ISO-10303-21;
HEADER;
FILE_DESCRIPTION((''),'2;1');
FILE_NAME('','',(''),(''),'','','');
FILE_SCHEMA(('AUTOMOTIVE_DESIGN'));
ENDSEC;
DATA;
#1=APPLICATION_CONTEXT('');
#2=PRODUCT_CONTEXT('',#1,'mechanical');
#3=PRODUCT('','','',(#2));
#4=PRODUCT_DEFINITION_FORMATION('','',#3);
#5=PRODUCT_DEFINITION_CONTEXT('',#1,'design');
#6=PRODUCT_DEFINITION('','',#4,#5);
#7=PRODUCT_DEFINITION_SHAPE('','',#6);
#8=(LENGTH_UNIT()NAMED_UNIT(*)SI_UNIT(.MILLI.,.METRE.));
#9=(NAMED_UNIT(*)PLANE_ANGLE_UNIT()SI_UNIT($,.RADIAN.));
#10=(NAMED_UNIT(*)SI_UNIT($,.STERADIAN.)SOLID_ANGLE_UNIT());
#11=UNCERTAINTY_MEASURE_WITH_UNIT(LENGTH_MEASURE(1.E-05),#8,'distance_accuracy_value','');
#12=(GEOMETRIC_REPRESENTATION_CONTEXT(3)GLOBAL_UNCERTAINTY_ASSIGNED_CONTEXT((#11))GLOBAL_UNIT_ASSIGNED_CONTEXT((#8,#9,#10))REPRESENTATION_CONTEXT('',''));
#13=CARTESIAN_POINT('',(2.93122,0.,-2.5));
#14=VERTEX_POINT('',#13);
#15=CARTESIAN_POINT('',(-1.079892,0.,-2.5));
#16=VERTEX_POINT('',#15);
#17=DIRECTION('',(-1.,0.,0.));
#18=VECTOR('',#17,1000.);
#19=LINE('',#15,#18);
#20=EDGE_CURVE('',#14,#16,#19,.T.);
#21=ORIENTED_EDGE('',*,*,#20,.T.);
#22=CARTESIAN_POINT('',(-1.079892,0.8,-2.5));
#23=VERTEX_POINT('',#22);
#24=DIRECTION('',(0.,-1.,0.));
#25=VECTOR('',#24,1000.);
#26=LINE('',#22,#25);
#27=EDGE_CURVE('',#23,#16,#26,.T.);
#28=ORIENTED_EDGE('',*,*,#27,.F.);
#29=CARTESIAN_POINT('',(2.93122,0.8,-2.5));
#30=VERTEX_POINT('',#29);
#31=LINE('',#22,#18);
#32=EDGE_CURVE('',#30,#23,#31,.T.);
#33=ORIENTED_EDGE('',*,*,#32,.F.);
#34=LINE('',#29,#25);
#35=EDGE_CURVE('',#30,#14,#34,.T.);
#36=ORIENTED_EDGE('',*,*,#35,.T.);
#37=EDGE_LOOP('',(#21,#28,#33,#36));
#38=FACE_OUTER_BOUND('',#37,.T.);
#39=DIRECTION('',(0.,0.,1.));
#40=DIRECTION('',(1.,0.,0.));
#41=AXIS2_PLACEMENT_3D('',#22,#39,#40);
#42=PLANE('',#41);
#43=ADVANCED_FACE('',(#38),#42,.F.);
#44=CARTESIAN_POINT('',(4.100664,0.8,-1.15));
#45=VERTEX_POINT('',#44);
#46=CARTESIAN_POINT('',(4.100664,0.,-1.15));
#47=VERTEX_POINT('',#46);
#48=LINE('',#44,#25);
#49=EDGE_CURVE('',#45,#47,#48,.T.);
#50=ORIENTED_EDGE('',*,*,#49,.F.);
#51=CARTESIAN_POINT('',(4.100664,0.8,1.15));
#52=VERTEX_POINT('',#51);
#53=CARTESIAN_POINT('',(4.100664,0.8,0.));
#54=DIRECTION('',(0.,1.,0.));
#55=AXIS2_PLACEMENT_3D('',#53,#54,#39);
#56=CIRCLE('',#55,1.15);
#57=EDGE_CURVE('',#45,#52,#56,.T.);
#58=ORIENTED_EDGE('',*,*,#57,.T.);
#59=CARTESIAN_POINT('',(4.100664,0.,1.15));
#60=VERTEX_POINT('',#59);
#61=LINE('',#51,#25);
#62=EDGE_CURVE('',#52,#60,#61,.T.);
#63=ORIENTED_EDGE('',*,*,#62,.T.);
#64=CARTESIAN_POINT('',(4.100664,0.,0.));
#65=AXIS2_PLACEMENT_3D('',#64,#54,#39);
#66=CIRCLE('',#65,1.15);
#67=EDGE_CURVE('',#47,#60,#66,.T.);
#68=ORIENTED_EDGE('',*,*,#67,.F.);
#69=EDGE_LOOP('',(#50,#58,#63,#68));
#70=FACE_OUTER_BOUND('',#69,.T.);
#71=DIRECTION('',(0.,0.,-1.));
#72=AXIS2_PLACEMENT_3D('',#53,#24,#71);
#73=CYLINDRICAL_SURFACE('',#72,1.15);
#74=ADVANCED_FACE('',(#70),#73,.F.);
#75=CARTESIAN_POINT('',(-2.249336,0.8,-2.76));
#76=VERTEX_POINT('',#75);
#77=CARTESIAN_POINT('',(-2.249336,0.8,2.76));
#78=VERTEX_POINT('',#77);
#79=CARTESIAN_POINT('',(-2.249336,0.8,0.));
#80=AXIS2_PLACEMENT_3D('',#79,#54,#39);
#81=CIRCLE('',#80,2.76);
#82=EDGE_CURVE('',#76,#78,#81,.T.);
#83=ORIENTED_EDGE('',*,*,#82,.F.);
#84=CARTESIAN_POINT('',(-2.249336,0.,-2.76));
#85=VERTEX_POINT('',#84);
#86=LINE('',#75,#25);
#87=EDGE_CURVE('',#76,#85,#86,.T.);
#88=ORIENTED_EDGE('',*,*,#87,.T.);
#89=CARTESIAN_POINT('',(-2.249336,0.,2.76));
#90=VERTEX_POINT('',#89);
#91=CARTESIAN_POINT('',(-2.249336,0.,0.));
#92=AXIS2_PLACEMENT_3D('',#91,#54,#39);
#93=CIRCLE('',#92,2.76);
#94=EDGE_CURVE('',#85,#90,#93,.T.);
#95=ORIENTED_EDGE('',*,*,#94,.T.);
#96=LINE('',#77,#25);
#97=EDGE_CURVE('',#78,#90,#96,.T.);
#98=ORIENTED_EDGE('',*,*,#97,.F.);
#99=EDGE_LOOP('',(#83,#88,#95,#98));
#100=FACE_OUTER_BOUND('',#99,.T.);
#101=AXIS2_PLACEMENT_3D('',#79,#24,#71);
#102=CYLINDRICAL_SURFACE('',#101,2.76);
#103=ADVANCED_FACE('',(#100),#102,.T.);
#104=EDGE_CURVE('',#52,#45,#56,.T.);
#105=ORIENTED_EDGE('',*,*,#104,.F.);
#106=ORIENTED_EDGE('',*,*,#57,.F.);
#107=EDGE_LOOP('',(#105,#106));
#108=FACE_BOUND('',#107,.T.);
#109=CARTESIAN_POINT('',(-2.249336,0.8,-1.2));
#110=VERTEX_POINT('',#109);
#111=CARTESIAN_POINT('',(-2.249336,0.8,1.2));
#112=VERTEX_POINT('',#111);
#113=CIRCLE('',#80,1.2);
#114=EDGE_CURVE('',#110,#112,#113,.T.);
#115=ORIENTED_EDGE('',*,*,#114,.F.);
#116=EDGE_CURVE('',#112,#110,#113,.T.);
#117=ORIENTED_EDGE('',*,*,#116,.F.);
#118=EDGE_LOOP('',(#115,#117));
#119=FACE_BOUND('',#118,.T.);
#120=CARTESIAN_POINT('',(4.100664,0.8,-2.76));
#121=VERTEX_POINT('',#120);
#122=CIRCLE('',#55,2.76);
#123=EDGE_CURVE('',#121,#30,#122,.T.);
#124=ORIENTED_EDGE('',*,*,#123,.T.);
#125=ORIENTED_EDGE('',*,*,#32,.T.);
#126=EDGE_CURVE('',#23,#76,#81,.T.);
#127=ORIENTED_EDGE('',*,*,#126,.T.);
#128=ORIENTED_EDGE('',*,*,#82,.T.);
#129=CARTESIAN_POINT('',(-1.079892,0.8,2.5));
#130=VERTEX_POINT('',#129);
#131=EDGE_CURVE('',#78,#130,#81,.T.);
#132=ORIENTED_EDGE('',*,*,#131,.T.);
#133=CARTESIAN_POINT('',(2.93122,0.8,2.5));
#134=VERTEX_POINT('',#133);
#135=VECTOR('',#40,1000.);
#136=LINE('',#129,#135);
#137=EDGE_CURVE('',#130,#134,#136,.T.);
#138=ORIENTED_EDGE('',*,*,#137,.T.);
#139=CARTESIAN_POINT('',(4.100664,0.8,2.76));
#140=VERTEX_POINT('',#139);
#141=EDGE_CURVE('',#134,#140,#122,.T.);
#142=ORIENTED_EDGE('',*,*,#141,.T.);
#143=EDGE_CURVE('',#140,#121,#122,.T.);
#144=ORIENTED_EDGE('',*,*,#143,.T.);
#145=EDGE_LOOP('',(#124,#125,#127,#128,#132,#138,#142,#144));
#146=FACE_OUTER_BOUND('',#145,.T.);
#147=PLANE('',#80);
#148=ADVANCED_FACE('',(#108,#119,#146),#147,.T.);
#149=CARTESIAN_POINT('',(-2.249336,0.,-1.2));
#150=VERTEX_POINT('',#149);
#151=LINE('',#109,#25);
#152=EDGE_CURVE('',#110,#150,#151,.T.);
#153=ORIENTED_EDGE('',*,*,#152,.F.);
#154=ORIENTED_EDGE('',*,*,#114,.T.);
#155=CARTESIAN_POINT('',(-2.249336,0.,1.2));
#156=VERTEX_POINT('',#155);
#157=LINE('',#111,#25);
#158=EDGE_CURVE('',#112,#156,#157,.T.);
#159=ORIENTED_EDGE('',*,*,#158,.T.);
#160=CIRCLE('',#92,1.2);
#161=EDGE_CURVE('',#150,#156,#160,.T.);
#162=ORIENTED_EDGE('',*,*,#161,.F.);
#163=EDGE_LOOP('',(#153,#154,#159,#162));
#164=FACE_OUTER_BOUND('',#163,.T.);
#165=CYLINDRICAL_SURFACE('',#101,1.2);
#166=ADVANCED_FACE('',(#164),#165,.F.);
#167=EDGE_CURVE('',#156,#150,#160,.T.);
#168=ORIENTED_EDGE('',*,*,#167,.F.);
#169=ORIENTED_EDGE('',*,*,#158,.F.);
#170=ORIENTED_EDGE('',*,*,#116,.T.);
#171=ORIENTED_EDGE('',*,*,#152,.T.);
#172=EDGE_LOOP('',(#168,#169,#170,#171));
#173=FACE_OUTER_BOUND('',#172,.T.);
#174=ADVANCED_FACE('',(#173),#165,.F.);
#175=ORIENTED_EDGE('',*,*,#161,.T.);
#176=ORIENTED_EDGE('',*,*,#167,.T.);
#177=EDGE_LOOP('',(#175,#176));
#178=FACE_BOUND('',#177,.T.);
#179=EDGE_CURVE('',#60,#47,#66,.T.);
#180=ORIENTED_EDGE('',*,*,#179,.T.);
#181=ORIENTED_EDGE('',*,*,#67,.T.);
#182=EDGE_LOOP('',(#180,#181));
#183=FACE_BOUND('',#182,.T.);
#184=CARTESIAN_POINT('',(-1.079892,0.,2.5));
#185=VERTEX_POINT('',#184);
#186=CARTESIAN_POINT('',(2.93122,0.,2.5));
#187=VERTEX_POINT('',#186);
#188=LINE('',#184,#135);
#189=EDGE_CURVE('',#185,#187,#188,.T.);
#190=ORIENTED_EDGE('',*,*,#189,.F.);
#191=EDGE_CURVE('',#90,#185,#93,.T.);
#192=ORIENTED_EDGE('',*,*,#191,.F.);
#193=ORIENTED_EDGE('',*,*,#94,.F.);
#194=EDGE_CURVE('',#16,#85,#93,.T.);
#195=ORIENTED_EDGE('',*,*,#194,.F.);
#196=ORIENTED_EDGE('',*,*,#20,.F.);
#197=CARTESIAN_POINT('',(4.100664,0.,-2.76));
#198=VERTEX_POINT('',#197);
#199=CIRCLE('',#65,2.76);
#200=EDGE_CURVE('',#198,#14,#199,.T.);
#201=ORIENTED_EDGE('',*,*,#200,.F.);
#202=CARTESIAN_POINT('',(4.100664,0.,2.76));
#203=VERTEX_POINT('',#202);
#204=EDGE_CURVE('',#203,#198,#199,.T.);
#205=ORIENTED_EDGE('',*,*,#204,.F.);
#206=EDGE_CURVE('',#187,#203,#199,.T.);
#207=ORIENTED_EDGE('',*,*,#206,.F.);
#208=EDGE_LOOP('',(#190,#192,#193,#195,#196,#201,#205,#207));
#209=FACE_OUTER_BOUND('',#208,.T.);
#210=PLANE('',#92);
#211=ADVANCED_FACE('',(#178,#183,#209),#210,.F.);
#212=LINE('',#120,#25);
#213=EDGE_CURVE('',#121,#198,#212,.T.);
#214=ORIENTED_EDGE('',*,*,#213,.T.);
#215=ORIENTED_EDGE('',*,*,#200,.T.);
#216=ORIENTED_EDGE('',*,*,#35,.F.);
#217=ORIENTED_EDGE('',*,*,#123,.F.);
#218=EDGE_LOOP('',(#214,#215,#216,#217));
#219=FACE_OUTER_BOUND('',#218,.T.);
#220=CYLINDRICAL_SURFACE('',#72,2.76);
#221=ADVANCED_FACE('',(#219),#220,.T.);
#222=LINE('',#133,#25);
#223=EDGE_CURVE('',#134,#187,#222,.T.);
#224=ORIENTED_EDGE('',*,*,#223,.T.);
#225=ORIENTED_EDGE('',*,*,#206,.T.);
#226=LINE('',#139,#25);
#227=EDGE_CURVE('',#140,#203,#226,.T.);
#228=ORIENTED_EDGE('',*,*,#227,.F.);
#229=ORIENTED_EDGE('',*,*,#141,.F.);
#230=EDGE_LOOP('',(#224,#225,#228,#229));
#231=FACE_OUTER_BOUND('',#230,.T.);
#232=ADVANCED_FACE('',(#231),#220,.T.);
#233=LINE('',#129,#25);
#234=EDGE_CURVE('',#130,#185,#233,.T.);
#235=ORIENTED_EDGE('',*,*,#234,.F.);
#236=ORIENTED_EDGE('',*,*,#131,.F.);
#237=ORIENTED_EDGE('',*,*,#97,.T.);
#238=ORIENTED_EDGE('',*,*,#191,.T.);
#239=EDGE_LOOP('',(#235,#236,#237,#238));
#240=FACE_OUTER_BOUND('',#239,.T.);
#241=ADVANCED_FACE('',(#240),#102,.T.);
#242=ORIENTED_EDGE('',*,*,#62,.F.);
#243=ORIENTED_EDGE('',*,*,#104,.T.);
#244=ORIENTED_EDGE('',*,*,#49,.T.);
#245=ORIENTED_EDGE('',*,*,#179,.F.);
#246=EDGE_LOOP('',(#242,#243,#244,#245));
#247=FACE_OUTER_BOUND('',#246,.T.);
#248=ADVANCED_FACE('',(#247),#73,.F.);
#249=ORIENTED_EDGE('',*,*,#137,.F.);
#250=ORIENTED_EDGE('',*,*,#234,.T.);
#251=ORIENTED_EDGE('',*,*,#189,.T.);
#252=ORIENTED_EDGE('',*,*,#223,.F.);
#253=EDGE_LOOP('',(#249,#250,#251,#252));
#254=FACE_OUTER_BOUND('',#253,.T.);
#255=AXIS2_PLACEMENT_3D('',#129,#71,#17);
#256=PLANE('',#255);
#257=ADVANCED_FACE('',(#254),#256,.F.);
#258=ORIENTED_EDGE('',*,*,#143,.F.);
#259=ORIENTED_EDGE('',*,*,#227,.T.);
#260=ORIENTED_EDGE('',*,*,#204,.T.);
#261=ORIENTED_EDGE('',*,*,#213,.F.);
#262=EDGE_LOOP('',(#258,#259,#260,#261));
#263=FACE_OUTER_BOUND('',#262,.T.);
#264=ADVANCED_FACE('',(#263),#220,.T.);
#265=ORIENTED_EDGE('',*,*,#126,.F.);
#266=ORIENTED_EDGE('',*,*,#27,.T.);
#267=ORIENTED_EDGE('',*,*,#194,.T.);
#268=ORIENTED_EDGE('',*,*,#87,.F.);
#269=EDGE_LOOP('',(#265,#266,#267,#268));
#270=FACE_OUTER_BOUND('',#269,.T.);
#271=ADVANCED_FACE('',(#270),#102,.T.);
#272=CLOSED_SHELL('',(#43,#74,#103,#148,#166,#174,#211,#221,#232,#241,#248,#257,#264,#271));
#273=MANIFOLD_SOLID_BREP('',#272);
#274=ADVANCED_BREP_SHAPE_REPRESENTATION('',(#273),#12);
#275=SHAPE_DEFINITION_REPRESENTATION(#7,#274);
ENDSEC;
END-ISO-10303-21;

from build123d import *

# Parameters (mm, degrees)
SKETCH_1_R      = 1.2
SKETCH_1_R_2    = 1.15
EXTRUDE_1_DEPTH = 0.8


with BuildPart() as part:
    # 草图1 → 凸台-拉伸1 (new body)
    with BuildSketch(Plane(origin=(0, 0, 0), x_dir=(1, 0, 0), z_dir=(0, 1, 0))):
        with BuildLine():
            Line((-1.079891697, 2.5), (2.931219678, 2.5))
            ThreePointArc((2.931219678, 2.5), (6.860663991, 0), (2.931219678, -2.5))
            Line((2.931219678, -2.5), (-1.079891697, -2.5))
            ThreePointArc((-1.079891697, -2.5), (-5.009336009, 0), (-1.079891697, 2.5))
        make_face()
        with Locations(Location((-2.249336009, 0, 0), (0, 0, 270))):
            Circle(SKETCH_1_R, mode=Mode.SUBTRACT)
        with Locations(Location((4.100663991, 0, 0), (0, 0, 270))):
            Circle(SKETCH_1_R_2, mode=Mode.SUBTRACT)
    extrude(amount=EXTRUDE_1_DEPTH)


solid = part.part
